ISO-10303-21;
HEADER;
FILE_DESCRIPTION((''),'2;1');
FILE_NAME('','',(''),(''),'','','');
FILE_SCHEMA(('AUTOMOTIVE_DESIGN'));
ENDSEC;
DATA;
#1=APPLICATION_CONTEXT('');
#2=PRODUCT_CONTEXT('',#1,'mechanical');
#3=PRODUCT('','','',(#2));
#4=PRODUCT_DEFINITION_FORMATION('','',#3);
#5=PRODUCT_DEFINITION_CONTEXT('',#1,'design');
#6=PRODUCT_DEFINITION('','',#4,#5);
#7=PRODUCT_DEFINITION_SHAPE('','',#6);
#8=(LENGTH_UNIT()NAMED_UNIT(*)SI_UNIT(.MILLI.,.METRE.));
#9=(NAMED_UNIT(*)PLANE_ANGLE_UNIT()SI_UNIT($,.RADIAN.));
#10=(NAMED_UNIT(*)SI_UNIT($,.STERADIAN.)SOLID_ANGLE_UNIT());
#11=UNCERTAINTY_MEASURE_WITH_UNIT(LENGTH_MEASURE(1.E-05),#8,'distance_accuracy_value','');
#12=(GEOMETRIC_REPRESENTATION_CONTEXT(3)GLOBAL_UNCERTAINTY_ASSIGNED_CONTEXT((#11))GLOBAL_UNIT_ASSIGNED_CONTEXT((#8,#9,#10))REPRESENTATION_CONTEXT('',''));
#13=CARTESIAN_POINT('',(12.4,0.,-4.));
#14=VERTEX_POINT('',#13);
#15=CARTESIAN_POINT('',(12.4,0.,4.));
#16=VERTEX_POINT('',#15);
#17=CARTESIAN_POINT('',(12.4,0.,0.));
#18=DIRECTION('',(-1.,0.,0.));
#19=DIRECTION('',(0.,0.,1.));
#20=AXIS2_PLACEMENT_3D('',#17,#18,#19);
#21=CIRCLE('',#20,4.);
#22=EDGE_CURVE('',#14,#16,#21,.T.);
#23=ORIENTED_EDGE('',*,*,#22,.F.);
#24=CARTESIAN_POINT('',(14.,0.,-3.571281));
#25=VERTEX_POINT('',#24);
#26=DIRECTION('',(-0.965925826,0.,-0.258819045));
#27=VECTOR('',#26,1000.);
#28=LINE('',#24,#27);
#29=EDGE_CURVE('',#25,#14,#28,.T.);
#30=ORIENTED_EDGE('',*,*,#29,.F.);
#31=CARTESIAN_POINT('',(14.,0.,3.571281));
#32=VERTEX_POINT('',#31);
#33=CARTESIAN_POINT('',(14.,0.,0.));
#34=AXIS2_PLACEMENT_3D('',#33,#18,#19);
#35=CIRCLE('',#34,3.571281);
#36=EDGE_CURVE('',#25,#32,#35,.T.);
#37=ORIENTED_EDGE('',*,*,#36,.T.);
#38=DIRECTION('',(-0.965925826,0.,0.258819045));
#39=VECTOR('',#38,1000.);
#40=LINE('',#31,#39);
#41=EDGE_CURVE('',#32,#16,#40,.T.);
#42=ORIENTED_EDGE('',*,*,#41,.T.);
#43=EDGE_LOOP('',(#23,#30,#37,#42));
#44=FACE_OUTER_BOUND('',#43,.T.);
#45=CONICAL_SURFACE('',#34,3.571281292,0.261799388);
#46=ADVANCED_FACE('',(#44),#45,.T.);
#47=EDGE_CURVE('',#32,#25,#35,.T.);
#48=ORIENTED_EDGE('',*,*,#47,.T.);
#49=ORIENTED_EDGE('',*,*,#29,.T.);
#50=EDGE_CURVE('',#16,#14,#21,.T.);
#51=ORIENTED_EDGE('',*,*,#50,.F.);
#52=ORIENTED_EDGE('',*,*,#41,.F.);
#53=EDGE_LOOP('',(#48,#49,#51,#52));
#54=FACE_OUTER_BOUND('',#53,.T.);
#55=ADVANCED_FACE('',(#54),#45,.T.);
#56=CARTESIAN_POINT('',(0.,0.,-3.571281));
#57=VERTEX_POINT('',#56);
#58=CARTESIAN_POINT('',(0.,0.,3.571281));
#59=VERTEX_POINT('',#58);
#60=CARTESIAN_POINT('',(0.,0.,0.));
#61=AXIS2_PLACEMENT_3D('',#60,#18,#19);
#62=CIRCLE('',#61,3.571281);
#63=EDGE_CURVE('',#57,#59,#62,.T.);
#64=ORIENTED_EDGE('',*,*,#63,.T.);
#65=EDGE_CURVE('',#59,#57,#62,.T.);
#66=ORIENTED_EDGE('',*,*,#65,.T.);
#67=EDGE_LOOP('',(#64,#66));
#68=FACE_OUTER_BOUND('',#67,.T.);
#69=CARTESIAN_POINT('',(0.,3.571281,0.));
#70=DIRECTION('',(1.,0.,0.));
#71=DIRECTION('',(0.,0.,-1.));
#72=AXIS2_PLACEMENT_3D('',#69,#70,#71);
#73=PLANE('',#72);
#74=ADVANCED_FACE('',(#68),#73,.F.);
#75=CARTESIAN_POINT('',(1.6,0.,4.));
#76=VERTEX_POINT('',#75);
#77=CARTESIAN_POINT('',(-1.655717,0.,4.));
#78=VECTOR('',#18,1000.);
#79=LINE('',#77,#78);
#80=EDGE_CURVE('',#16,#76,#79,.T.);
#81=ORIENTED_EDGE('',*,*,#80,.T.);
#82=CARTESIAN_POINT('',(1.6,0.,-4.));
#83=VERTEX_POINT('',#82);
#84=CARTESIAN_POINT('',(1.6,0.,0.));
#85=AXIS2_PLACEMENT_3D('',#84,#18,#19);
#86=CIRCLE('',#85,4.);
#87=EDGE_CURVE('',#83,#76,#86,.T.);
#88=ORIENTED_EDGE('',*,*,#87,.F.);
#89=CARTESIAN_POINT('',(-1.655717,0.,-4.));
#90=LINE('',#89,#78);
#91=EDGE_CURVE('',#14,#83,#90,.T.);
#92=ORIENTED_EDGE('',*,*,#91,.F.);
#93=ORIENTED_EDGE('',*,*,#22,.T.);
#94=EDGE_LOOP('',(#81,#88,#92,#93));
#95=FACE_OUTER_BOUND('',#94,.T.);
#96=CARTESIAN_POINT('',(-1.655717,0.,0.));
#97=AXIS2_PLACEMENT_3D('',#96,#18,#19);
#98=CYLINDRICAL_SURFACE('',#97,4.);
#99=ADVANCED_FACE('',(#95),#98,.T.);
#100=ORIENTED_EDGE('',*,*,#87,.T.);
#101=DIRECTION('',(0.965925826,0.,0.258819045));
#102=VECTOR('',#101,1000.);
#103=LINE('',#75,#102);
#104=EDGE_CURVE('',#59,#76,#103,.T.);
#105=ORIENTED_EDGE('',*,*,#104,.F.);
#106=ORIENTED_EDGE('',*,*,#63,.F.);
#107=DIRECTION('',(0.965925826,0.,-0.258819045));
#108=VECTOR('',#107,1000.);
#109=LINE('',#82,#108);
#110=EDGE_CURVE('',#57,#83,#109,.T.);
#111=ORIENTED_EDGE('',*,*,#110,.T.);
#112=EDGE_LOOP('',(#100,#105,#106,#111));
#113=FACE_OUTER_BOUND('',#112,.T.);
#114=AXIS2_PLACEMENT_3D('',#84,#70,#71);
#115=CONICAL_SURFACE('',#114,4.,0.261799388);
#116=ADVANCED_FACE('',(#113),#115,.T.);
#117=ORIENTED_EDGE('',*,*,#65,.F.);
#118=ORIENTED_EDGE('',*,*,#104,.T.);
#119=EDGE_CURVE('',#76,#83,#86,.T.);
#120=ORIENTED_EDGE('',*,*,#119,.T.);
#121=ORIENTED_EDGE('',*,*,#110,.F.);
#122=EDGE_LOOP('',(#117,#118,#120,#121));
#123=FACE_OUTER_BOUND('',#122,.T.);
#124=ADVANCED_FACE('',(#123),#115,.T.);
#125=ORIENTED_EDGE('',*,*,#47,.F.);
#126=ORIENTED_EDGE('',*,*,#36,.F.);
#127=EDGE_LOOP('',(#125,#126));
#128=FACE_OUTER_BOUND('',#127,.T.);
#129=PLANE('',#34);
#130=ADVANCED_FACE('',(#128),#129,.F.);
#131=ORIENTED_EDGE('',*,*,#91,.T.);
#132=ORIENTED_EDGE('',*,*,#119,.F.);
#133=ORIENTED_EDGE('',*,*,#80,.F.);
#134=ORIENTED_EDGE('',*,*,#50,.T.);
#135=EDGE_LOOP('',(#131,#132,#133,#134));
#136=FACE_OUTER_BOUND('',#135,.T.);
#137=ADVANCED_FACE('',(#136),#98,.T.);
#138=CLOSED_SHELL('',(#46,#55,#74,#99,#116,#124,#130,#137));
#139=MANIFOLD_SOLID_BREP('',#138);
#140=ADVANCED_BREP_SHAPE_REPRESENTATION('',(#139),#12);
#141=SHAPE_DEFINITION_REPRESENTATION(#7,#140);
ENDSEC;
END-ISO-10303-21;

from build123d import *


with BuildPart() as part:
    # Sketch1 → Base-Revolve (revolve)
    with BuildSketch(Plane.XY, mode=Mode.PRIVATE) as base_revolve_sk:
        Polygon((0, 0), (14, 0), (14, 3.571281292), (12.4, 4), (1.6, 4), (0, 3.571281292), align=None)
    revolve(base_revolve_sk.sketch.rotate(Axis((-1.655717266, 0, 0), (1, 0, 0)), 90), axis=Axis((-1.655717266, 0, 0), (1, 0, 0)))


solid = part.part
